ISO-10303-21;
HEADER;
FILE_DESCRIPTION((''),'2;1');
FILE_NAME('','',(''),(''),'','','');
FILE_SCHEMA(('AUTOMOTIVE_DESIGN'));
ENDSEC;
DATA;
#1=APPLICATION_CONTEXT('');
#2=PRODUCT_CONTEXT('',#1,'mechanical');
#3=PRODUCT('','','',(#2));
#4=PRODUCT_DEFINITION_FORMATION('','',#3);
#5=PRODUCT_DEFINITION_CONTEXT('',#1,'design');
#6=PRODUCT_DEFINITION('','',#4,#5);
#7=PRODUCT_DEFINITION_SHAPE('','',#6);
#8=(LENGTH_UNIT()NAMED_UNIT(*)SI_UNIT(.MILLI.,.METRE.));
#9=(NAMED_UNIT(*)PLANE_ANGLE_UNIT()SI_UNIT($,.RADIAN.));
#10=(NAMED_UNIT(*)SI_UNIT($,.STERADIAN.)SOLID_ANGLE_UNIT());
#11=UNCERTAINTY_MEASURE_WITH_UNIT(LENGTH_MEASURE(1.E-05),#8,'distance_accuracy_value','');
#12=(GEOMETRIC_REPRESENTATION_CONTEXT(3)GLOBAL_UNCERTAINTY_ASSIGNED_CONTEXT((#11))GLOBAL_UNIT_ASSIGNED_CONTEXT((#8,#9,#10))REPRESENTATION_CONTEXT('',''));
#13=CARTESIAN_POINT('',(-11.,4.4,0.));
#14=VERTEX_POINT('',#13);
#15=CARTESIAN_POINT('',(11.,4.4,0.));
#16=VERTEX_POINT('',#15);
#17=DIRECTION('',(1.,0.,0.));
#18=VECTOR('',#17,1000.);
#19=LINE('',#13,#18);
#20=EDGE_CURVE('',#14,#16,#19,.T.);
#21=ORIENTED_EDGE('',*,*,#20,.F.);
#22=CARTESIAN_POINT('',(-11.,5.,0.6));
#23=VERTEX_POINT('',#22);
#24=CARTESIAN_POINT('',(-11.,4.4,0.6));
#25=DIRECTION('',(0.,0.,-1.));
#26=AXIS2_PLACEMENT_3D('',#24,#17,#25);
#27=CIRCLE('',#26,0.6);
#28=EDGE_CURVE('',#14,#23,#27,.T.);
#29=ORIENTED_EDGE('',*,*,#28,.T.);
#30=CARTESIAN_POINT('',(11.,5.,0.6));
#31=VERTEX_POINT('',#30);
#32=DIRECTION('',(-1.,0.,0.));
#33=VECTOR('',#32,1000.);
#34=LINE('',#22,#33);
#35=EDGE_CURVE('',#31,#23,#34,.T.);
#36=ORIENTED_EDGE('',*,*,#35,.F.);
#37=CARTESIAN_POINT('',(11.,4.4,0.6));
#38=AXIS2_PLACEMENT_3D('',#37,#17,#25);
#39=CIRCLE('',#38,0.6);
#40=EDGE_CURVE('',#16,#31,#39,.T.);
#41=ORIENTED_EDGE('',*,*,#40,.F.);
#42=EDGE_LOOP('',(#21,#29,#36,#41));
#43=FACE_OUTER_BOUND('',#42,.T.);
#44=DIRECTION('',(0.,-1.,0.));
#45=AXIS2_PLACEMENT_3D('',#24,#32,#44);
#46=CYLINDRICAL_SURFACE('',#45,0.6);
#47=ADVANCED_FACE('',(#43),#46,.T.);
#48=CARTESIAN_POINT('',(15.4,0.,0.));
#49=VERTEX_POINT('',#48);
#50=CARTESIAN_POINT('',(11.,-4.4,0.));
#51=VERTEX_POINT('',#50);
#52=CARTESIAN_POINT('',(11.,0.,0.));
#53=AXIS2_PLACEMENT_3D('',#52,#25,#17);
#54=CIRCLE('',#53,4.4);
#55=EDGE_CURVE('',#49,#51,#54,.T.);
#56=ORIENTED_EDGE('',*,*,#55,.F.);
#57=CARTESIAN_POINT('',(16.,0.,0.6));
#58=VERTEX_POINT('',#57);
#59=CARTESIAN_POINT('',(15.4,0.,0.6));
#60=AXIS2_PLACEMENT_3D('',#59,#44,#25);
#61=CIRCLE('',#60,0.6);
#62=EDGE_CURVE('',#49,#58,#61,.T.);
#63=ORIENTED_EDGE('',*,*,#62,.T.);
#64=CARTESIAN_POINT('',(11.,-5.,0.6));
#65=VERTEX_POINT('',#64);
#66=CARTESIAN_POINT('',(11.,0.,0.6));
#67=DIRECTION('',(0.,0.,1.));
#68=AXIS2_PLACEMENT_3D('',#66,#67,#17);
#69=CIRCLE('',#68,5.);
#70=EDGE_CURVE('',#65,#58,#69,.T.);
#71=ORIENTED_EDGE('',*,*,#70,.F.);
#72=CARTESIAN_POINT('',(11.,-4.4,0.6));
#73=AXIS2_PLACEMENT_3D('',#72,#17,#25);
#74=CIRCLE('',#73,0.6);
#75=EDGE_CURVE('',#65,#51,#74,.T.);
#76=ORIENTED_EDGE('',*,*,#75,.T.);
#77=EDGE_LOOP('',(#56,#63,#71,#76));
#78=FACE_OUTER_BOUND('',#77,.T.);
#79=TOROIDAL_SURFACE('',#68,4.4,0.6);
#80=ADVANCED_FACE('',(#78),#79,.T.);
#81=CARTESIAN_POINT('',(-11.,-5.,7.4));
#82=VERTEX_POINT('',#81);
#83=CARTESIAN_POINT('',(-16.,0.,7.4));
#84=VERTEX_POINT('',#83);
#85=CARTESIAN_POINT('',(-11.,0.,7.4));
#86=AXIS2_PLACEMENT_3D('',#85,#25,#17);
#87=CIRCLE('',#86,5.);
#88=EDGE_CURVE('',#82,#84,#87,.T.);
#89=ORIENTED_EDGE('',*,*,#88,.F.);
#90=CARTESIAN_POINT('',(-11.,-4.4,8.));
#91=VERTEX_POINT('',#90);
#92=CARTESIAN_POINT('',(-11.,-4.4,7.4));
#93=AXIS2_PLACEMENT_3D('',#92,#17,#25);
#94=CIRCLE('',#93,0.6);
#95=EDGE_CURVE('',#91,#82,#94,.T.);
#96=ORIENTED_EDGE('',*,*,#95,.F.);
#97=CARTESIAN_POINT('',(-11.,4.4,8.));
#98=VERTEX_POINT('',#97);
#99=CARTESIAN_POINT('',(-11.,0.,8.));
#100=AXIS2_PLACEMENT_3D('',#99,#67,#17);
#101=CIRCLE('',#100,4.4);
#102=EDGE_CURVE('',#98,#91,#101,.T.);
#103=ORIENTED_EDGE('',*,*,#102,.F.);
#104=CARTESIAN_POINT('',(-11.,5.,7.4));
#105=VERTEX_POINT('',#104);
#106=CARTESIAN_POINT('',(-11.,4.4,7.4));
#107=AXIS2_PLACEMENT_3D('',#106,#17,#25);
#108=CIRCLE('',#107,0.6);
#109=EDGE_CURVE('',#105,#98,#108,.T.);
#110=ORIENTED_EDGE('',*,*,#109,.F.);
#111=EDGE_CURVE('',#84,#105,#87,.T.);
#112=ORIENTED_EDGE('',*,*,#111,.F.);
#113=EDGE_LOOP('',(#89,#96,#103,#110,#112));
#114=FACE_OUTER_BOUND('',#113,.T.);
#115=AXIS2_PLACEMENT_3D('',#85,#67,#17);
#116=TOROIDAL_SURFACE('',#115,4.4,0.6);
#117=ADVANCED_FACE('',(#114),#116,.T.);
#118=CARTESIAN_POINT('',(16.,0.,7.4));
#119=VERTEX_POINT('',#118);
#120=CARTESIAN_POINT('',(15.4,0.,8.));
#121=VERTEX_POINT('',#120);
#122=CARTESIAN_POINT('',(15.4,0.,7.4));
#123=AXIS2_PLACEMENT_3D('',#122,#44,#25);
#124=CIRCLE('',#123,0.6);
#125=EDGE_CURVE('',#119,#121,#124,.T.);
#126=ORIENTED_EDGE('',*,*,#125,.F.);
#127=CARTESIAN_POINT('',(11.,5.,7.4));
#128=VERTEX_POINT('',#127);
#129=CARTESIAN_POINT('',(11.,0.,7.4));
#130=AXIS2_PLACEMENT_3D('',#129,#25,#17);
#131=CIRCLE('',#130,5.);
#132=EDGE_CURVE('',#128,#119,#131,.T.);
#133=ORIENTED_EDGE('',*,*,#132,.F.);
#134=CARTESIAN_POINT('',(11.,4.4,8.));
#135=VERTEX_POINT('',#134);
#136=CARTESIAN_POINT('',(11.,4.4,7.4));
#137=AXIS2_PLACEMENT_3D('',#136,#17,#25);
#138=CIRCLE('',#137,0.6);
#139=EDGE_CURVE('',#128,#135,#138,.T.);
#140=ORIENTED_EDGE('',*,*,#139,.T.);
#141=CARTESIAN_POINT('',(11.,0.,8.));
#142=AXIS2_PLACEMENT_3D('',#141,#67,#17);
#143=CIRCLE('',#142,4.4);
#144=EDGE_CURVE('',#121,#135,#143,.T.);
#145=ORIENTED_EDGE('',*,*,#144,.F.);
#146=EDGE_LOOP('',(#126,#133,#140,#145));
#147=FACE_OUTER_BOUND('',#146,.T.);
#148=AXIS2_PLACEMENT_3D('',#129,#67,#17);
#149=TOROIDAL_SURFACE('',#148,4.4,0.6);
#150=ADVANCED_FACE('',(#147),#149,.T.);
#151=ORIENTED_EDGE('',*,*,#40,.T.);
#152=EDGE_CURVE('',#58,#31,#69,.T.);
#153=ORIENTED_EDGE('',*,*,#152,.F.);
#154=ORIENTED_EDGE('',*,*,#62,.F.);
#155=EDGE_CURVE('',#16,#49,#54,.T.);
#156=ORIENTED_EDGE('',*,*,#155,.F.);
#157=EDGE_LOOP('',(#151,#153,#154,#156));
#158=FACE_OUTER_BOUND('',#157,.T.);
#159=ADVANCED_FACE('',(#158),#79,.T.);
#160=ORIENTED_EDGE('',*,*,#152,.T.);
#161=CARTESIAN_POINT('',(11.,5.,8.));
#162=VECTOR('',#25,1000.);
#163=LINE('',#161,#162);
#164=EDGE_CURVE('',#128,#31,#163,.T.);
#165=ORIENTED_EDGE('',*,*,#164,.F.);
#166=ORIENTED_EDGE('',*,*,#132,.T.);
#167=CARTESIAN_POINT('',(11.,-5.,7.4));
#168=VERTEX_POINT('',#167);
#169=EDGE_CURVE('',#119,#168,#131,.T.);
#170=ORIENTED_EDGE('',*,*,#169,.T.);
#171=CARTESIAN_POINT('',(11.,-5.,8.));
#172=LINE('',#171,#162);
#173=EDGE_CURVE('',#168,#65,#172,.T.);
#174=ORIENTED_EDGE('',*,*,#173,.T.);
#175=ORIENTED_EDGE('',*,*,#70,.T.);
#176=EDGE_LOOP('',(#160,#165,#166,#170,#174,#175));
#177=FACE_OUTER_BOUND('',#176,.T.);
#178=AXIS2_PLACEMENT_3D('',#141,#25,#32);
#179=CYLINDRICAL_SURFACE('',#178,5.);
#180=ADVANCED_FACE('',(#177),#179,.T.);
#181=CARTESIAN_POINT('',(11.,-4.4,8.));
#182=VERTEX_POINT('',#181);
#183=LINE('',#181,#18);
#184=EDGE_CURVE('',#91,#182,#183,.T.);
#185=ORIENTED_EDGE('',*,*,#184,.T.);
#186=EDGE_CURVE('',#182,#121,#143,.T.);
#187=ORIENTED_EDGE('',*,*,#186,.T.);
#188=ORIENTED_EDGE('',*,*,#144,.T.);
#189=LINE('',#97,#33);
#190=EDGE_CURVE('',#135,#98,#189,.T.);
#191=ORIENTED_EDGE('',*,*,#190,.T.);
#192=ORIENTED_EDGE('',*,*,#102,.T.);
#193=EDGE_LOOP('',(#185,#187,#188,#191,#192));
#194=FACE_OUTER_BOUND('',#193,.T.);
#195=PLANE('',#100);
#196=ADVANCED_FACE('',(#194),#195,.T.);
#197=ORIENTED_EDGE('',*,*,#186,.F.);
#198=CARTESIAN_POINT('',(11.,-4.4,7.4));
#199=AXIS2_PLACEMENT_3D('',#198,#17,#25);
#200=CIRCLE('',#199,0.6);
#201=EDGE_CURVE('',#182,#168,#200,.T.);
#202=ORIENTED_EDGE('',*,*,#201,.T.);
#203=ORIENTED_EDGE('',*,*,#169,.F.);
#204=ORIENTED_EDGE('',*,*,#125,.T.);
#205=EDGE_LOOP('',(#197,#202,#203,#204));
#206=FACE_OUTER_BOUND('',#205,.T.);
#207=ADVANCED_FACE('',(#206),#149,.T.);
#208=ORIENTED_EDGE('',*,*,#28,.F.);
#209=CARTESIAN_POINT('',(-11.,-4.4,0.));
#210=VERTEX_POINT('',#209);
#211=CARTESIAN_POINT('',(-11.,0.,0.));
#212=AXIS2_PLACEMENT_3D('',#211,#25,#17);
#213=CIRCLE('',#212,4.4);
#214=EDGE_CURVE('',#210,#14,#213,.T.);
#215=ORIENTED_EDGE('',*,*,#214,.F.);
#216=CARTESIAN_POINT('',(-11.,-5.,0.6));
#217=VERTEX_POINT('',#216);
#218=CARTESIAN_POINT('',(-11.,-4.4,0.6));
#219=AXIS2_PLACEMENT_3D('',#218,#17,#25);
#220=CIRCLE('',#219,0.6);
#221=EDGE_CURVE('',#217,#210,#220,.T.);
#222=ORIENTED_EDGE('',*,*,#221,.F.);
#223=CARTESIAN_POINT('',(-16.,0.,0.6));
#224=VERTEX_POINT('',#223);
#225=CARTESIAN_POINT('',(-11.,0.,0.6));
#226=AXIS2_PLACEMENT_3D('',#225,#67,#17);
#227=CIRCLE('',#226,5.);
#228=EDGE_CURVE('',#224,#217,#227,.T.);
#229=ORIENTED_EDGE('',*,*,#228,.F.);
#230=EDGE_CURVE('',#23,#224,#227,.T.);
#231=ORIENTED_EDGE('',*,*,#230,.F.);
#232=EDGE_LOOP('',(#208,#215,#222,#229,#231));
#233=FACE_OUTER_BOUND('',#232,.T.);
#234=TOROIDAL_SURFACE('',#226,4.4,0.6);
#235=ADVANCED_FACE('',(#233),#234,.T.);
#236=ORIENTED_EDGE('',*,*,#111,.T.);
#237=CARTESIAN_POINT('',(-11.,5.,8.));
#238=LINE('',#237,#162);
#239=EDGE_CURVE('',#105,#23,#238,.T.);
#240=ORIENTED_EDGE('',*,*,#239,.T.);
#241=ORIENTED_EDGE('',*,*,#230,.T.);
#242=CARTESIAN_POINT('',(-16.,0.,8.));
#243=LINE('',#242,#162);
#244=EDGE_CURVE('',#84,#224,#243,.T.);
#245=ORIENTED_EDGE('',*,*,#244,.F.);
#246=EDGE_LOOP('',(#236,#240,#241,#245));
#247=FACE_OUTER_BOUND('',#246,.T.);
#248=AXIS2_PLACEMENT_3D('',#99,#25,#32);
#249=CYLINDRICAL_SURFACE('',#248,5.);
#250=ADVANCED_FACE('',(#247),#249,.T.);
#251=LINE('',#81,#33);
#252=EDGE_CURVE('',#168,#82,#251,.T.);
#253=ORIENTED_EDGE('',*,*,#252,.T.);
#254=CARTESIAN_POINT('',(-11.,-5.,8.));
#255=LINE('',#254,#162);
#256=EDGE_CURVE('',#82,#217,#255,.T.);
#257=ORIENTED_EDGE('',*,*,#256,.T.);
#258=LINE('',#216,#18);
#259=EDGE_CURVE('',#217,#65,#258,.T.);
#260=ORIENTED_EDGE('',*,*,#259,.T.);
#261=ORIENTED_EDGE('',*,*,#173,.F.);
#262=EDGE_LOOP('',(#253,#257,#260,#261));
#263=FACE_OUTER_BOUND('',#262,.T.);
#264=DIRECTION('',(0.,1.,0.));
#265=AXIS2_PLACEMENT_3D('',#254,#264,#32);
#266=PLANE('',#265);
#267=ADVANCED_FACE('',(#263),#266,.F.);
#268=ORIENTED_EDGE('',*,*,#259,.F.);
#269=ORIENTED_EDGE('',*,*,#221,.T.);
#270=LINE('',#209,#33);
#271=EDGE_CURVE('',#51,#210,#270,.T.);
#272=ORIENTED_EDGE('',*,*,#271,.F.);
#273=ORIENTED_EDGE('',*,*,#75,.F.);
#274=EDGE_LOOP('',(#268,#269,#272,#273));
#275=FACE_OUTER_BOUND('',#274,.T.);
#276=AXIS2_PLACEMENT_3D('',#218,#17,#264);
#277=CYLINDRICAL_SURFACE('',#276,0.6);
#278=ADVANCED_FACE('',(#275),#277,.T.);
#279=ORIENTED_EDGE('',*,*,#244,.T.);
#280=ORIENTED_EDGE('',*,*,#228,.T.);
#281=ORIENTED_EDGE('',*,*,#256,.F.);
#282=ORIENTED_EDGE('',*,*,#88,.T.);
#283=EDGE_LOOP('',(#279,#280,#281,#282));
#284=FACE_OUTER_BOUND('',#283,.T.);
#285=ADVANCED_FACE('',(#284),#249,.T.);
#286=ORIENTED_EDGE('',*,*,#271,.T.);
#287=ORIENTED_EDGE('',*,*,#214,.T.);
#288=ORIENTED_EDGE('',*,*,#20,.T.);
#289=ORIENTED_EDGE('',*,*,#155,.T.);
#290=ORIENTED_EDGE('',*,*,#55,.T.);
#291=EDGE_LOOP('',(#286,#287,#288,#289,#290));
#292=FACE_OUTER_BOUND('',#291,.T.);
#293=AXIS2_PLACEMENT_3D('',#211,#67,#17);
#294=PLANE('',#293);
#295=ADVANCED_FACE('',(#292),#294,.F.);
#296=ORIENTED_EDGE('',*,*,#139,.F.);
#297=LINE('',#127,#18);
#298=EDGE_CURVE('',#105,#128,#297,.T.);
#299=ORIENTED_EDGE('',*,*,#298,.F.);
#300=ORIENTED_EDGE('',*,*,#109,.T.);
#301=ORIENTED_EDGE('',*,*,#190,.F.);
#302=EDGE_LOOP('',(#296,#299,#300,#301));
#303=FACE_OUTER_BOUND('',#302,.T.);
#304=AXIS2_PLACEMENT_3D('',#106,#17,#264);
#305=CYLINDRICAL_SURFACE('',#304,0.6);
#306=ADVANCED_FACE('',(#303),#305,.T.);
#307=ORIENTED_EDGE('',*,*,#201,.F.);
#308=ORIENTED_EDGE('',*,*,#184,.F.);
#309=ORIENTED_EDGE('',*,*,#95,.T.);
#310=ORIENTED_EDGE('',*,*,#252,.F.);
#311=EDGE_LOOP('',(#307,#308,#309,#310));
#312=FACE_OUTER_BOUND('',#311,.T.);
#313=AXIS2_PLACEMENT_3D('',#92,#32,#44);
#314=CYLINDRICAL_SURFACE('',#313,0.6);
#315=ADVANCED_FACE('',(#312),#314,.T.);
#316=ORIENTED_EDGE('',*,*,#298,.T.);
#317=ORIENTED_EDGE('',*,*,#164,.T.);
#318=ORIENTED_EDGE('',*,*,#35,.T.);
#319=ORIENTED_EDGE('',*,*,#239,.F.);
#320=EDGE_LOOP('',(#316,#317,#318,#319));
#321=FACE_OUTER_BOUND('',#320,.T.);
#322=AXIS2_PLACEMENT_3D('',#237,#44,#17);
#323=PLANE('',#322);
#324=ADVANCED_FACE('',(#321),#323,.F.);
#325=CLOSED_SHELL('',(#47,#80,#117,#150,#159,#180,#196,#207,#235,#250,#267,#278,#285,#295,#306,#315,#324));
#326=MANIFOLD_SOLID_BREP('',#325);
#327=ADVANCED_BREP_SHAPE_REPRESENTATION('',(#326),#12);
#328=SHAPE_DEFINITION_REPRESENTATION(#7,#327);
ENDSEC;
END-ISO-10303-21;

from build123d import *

# Parameters (mm, degrees)
EXTRUDE_523_DEPTH = 8
FILLET_1_R        = 0.6


with BuildPart() as part:
    # 草图1 → Extrude 523 (new body)
    with BuildSketch(Plane.XY):
        with BuildLine():
            Line((-11, 5), (11, 5))
            ThreePointArc((11, 5), (16, 0), (11, -5))
            Line((11, -5), (-11, -5))
            ThreePointArc((-11, -5), (-16, 0), (-11, 5))
        make_face()
    extrude(amount=EXTRUDE_523_DEPTH)

    # 圆角1
    fillet_1_edges = [part.edges().sort_by_distance(p)[0] for p in [
        (16, 0, 8),
        (0, 5, 8),
        (-16, 0, 8),
        (0, 5, 0),
        (16, 0, 0),
        (0, -5, 0),
        (-16, 0, 0),
        (0, -5, 8),
    ]]
    fillet(fillet_1_edges, radius=FILLET_1_R)


solid = part.part
